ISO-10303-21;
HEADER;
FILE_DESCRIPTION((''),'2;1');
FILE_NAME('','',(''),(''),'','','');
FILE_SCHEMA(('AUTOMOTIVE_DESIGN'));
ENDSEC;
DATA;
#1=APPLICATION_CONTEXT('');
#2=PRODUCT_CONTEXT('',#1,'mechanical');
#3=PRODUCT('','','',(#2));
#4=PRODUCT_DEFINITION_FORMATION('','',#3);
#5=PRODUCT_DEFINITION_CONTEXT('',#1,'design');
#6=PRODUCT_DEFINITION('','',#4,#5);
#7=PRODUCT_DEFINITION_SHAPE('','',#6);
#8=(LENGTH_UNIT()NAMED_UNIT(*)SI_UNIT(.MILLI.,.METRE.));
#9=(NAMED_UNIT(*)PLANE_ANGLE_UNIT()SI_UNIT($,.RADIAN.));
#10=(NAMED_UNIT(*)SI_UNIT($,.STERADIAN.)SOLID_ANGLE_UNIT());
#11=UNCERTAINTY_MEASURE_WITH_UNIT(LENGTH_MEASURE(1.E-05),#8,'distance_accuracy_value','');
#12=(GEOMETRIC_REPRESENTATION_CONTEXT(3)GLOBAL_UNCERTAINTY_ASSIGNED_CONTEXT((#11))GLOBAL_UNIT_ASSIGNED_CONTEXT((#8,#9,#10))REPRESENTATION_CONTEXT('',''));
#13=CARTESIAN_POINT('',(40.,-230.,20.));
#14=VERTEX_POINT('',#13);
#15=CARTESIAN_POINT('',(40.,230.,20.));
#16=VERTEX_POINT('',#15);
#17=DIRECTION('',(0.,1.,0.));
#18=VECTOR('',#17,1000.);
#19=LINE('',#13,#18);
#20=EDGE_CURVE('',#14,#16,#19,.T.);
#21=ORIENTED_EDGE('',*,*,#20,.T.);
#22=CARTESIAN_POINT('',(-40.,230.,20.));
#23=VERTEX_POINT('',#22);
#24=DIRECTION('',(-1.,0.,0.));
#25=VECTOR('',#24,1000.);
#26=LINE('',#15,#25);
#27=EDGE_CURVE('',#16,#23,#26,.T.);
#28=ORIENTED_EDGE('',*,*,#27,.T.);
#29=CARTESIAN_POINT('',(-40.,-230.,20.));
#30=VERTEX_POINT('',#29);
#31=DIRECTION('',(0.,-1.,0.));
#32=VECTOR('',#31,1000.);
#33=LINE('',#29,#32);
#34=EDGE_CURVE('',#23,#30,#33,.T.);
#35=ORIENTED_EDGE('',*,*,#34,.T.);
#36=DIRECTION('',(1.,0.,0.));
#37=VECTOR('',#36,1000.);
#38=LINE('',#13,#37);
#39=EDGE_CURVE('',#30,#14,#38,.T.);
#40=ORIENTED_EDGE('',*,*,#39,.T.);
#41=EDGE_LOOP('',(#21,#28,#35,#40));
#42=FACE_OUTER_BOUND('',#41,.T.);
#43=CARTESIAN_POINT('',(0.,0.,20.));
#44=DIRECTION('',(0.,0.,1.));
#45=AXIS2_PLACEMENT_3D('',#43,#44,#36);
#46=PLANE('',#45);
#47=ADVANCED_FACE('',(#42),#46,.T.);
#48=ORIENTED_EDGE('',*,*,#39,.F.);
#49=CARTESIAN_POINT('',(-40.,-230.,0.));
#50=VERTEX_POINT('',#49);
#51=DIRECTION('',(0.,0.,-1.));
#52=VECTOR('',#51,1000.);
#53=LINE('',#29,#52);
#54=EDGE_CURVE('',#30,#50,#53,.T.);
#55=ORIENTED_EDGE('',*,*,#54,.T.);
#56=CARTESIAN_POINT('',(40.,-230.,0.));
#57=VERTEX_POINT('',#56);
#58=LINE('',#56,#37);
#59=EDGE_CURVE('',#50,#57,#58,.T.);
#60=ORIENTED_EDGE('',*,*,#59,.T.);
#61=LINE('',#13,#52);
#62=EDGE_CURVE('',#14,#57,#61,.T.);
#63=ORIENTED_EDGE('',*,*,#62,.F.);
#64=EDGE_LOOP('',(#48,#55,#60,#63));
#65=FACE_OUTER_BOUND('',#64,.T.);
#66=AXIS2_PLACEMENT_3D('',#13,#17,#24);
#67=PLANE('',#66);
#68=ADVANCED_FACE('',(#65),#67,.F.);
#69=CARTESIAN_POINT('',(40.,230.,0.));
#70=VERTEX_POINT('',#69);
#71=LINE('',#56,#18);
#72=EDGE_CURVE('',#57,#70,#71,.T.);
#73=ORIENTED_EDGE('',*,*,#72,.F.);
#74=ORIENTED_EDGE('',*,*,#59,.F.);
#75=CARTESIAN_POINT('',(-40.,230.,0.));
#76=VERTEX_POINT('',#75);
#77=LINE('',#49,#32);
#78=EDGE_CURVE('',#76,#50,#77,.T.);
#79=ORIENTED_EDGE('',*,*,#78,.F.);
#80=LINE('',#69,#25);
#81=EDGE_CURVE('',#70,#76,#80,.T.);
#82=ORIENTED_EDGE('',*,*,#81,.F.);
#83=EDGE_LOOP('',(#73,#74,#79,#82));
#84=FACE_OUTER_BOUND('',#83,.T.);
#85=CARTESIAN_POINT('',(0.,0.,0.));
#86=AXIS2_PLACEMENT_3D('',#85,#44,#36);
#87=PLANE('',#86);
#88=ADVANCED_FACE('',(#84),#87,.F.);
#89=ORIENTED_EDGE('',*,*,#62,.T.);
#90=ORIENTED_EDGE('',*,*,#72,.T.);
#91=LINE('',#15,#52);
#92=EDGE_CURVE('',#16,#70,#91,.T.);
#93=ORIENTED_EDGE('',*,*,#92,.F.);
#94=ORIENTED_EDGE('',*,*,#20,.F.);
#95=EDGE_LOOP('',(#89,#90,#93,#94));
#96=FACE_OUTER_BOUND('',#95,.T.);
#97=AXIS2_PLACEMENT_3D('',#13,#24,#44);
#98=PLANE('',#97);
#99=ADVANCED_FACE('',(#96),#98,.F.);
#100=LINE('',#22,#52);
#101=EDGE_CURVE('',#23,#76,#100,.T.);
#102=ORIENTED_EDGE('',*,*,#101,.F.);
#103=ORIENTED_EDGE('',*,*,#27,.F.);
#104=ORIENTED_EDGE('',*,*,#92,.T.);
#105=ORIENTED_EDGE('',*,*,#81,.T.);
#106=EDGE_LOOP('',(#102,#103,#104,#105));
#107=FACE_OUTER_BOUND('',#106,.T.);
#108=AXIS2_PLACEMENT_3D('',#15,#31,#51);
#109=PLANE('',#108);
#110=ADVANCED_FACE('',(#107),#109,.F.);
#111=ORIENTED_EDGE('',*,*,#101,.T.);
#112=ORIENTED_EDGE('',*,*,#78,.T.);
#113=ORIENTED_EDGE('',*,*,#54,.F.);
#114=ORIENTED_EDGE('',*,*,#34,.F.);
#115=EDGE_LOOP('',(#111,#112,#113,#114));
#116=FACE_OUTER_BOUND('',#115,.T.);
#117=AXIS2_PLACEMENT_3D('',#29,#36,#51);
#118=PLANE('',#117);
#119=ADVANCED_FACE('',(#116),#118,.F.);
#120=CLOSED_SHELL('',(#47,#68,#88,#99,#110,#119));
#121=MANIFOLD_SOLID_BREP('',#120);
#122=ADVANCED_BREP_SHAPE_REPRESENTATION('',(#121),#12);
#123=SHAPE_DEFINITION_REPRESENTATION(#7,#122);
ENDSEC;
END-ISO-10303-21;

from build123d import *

# Parameters (mm, degrees)
SKETCH1_W           = 80
SKETCH1_H           = 460
BOSS_EXTRUDE1_DEPTH = 20


with BuildPart() as part:
    # Sketch1 → Boss-Extrude1 (new body)
    with BuildSketch(Plane.XY):
        Rectangle(SKETCH1_W, SKETCH1_H)
    extrude(amount=BOSS_EXTRUDE1_DEPTH)


solid = part.part
